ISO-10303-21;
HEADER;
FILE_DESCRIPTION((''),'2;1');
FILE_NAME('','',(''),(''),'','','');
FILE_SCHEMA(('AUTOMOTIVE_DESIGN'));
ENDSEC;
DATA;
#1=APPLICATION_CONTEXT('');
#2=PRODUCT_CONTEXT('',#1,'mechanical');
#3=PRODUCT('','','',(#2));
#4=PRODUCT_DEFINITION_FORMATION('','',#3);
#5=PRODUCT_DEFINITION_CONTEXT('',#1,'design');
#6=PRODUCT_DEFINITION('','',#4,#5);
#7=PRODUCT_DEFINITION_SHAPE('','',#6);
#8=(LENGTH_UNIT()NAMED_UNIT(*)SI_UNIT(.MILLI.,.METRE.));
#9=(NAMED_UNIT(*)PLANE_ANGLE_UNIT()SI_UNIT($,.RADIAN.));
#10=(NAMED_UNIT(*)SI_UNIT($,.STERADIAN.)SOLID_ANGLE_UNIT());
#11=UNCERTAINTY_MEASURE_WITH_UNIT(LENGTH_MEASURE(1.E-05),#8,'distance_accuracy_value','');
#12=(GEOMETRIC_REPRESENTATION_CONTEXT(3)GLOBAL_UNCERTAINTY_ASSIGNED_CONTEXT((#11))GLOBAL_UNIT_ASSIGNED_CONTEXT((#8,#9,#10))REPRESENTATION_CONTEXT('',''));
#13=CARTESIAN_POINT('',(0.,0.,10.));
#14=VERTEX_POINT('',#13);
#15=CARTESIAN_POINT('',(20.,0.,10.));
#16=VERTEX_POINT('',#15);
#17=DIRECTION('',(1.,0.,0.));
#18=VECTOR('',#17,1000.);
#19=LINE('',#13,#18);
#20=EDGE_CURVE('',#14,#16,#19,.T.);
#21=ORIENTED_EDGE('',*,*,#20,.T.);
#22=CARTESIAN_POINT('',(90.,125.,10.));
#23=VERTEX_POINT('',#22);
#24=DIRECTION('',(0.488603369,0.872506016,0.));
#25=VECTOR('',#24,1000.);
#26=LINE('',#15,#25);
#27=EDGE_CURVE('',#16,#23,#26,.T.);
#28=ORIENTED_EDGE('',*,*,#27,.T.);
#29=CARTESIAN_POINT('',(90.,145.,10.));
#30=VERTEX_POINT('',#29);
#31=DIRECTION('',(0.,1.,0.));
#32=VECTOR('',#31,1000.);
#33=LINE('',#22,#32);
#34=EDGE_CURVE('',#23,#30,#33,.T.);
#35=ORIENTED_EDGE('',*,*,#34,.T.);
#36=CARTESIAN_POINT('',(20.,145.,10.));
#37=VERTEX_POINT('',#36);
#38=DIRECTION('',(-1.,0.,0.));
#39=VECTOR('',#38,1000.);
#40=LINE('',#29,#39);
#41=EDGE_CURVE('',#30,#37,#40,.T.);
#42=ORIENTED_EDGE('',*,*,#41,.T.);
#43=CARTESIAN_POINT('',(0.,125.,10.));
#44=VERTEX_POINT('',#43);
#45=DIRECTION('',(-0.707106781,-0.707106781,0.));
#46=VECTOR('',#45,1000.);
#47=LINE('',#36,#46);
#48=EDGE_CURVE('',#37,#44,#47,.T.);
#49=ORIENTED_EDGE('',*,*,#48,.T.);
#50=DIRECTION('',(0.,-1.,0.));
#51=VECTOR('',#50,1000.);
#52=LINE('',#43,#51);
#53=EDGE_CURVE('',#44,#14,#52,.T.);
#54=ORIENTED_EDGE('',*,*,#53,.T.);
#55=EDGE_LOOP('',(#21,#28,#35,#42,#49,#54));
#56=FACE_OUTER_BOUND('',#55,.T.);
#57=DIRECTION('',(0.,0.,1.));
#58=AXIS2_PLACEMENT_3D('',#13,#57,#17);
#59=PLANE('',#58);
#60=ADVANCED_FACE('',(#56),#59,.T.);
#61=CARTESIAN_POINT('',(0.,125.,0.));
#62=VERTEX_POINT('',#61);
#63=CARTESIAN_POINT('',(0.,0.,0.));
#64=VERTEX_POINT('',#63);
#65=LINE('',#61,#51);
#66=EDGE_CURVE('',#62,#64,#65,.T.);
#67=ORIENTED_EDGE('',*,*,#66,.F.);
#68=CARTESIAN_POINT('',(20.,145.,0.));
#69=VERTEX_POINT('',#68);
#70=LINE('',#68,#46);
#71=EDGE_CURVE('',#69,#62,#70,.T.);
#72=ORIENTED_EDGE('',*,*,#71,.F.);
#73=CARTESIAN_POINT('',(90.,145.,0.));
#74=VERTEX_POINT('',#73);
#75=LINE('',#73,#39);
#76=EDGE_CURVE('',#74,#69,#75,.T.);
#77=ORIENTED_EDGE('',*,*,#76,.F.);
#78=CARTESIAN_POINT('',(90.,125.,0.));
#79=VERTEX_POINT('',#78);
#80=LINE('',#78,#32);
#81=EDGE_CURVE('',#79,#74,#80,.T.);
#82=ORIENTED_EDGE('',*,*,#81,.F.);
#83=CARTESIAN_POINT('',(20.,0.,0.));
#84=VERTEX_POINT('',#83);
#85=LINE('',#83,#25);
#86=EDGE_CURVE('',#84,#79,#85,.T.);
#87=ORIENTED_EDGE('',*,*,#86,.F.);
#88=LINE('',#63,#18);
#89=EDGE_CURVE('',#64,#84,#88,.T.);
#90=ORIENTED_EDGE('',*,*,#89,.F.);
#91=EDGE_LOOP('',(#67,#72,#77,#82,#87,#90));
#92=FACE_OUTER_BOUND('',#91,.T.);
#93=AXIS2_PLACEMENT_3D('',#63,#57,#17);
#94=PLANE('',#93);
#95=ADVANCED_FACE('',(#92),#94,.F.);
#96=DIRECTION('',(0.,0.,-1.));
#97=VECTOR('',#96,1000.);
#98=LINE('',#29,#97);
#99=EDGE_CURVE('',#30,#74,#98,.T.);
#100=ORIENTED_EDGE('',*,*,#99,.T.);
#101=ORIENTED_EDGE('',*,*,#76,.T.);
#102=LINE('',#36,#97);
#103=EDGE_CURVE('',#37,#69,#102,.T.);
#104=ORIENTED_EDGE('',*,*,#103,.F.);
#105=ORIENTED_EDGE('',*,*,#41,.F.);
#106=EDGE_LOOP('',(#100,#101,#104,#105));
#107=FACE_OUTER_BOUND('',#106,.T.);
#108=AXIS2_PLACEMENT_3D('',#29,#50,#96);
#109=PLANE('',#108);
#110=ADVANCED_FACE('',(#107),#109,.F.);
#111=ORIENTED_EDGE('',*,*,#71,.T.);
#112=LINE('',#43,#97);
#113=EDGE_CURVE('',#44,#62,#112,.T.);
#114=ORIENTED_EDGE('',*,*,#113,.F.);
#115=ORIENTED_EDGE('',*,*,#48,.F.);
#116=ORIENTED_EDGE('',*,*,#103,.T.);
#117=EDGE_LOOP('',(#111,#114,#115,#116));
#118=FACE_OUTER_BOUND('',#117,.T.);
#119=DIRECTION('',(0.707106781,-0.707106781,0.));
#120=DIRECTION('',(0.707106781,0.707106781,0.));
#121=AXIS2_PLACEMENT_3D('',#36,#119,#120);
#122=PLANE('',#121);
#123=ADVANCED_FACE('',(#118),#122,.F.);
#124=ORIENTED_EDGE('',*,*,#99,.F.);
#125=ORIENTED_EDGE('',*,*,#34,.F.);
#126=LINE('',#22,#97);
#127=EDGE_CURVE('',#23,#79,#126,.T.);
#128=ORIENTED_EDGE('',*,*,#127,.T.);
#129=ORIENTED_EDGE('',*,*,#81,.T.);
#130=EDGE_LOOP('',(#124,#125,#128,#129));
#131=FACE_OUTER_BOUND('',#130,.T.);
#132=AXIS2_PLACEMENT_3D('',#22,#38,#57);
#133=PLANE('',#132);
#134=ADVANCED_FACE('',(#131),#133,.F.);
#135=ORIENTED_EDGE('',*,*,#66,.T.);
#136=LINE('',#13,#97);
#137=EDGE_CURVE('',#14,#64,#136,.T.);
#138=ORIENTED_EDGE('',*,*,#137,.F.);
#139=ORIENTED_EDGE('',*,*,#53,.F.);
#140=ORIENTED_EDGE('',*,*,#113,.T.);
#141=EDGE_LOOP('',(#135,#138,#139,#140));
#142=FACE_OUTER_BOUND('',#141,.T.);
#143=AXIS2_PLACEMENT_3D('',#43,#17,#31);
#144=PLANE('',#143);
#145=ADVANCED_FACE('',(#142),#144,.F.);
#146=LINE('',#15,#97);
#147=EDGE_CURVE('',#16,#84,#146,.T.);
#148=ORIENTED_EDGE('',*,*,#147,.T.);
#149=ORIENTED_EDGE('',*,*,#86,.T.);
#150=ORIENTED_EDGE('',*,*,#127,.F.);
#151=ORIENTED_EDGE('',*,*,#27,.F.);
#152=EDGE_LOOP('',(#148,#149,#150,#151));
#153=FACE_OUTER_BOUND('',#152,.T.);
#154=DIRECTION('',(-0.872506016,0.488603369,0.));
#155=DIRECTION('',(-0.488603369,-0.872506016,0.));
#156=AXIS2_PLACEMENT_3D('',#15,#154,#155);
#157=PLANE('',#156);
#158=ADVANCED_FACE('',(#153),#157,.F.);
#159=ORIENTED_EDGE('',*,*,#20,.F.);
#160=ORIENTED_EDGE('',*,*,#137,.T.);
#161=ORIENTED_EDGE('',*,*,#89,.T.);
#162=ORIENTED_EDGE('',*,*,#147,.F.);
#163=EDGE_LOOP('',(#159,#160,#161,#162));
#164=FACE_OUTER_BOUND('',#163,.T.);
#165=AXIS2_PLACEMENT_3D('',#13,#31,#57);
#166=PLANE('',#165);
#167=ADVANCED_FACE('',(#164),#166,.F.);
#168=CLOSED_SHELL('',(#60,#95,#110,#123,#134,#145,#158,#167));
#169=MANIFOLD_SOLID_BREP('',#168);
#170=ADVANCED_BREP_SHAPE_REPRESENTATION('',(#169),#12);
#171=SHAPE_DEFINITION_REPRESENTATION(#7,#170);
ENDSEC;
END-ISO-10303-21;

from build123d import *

# Parameters (mm, degrees)
BOSS_EXTRUDE1_DEPTH = 10


with BuildPart() as part:
    # Sketch1 → Boss-Extrude1 (new body)
    with BuildSketch(Plane.XY):
        Polygon((0, 0), (20, 0), (90, 125), (90, 145), (20, 145), (0, 125), align=None)
    extrude(amount=BOSS_EXTRUDE1_DEPTH)


solid = part.part
